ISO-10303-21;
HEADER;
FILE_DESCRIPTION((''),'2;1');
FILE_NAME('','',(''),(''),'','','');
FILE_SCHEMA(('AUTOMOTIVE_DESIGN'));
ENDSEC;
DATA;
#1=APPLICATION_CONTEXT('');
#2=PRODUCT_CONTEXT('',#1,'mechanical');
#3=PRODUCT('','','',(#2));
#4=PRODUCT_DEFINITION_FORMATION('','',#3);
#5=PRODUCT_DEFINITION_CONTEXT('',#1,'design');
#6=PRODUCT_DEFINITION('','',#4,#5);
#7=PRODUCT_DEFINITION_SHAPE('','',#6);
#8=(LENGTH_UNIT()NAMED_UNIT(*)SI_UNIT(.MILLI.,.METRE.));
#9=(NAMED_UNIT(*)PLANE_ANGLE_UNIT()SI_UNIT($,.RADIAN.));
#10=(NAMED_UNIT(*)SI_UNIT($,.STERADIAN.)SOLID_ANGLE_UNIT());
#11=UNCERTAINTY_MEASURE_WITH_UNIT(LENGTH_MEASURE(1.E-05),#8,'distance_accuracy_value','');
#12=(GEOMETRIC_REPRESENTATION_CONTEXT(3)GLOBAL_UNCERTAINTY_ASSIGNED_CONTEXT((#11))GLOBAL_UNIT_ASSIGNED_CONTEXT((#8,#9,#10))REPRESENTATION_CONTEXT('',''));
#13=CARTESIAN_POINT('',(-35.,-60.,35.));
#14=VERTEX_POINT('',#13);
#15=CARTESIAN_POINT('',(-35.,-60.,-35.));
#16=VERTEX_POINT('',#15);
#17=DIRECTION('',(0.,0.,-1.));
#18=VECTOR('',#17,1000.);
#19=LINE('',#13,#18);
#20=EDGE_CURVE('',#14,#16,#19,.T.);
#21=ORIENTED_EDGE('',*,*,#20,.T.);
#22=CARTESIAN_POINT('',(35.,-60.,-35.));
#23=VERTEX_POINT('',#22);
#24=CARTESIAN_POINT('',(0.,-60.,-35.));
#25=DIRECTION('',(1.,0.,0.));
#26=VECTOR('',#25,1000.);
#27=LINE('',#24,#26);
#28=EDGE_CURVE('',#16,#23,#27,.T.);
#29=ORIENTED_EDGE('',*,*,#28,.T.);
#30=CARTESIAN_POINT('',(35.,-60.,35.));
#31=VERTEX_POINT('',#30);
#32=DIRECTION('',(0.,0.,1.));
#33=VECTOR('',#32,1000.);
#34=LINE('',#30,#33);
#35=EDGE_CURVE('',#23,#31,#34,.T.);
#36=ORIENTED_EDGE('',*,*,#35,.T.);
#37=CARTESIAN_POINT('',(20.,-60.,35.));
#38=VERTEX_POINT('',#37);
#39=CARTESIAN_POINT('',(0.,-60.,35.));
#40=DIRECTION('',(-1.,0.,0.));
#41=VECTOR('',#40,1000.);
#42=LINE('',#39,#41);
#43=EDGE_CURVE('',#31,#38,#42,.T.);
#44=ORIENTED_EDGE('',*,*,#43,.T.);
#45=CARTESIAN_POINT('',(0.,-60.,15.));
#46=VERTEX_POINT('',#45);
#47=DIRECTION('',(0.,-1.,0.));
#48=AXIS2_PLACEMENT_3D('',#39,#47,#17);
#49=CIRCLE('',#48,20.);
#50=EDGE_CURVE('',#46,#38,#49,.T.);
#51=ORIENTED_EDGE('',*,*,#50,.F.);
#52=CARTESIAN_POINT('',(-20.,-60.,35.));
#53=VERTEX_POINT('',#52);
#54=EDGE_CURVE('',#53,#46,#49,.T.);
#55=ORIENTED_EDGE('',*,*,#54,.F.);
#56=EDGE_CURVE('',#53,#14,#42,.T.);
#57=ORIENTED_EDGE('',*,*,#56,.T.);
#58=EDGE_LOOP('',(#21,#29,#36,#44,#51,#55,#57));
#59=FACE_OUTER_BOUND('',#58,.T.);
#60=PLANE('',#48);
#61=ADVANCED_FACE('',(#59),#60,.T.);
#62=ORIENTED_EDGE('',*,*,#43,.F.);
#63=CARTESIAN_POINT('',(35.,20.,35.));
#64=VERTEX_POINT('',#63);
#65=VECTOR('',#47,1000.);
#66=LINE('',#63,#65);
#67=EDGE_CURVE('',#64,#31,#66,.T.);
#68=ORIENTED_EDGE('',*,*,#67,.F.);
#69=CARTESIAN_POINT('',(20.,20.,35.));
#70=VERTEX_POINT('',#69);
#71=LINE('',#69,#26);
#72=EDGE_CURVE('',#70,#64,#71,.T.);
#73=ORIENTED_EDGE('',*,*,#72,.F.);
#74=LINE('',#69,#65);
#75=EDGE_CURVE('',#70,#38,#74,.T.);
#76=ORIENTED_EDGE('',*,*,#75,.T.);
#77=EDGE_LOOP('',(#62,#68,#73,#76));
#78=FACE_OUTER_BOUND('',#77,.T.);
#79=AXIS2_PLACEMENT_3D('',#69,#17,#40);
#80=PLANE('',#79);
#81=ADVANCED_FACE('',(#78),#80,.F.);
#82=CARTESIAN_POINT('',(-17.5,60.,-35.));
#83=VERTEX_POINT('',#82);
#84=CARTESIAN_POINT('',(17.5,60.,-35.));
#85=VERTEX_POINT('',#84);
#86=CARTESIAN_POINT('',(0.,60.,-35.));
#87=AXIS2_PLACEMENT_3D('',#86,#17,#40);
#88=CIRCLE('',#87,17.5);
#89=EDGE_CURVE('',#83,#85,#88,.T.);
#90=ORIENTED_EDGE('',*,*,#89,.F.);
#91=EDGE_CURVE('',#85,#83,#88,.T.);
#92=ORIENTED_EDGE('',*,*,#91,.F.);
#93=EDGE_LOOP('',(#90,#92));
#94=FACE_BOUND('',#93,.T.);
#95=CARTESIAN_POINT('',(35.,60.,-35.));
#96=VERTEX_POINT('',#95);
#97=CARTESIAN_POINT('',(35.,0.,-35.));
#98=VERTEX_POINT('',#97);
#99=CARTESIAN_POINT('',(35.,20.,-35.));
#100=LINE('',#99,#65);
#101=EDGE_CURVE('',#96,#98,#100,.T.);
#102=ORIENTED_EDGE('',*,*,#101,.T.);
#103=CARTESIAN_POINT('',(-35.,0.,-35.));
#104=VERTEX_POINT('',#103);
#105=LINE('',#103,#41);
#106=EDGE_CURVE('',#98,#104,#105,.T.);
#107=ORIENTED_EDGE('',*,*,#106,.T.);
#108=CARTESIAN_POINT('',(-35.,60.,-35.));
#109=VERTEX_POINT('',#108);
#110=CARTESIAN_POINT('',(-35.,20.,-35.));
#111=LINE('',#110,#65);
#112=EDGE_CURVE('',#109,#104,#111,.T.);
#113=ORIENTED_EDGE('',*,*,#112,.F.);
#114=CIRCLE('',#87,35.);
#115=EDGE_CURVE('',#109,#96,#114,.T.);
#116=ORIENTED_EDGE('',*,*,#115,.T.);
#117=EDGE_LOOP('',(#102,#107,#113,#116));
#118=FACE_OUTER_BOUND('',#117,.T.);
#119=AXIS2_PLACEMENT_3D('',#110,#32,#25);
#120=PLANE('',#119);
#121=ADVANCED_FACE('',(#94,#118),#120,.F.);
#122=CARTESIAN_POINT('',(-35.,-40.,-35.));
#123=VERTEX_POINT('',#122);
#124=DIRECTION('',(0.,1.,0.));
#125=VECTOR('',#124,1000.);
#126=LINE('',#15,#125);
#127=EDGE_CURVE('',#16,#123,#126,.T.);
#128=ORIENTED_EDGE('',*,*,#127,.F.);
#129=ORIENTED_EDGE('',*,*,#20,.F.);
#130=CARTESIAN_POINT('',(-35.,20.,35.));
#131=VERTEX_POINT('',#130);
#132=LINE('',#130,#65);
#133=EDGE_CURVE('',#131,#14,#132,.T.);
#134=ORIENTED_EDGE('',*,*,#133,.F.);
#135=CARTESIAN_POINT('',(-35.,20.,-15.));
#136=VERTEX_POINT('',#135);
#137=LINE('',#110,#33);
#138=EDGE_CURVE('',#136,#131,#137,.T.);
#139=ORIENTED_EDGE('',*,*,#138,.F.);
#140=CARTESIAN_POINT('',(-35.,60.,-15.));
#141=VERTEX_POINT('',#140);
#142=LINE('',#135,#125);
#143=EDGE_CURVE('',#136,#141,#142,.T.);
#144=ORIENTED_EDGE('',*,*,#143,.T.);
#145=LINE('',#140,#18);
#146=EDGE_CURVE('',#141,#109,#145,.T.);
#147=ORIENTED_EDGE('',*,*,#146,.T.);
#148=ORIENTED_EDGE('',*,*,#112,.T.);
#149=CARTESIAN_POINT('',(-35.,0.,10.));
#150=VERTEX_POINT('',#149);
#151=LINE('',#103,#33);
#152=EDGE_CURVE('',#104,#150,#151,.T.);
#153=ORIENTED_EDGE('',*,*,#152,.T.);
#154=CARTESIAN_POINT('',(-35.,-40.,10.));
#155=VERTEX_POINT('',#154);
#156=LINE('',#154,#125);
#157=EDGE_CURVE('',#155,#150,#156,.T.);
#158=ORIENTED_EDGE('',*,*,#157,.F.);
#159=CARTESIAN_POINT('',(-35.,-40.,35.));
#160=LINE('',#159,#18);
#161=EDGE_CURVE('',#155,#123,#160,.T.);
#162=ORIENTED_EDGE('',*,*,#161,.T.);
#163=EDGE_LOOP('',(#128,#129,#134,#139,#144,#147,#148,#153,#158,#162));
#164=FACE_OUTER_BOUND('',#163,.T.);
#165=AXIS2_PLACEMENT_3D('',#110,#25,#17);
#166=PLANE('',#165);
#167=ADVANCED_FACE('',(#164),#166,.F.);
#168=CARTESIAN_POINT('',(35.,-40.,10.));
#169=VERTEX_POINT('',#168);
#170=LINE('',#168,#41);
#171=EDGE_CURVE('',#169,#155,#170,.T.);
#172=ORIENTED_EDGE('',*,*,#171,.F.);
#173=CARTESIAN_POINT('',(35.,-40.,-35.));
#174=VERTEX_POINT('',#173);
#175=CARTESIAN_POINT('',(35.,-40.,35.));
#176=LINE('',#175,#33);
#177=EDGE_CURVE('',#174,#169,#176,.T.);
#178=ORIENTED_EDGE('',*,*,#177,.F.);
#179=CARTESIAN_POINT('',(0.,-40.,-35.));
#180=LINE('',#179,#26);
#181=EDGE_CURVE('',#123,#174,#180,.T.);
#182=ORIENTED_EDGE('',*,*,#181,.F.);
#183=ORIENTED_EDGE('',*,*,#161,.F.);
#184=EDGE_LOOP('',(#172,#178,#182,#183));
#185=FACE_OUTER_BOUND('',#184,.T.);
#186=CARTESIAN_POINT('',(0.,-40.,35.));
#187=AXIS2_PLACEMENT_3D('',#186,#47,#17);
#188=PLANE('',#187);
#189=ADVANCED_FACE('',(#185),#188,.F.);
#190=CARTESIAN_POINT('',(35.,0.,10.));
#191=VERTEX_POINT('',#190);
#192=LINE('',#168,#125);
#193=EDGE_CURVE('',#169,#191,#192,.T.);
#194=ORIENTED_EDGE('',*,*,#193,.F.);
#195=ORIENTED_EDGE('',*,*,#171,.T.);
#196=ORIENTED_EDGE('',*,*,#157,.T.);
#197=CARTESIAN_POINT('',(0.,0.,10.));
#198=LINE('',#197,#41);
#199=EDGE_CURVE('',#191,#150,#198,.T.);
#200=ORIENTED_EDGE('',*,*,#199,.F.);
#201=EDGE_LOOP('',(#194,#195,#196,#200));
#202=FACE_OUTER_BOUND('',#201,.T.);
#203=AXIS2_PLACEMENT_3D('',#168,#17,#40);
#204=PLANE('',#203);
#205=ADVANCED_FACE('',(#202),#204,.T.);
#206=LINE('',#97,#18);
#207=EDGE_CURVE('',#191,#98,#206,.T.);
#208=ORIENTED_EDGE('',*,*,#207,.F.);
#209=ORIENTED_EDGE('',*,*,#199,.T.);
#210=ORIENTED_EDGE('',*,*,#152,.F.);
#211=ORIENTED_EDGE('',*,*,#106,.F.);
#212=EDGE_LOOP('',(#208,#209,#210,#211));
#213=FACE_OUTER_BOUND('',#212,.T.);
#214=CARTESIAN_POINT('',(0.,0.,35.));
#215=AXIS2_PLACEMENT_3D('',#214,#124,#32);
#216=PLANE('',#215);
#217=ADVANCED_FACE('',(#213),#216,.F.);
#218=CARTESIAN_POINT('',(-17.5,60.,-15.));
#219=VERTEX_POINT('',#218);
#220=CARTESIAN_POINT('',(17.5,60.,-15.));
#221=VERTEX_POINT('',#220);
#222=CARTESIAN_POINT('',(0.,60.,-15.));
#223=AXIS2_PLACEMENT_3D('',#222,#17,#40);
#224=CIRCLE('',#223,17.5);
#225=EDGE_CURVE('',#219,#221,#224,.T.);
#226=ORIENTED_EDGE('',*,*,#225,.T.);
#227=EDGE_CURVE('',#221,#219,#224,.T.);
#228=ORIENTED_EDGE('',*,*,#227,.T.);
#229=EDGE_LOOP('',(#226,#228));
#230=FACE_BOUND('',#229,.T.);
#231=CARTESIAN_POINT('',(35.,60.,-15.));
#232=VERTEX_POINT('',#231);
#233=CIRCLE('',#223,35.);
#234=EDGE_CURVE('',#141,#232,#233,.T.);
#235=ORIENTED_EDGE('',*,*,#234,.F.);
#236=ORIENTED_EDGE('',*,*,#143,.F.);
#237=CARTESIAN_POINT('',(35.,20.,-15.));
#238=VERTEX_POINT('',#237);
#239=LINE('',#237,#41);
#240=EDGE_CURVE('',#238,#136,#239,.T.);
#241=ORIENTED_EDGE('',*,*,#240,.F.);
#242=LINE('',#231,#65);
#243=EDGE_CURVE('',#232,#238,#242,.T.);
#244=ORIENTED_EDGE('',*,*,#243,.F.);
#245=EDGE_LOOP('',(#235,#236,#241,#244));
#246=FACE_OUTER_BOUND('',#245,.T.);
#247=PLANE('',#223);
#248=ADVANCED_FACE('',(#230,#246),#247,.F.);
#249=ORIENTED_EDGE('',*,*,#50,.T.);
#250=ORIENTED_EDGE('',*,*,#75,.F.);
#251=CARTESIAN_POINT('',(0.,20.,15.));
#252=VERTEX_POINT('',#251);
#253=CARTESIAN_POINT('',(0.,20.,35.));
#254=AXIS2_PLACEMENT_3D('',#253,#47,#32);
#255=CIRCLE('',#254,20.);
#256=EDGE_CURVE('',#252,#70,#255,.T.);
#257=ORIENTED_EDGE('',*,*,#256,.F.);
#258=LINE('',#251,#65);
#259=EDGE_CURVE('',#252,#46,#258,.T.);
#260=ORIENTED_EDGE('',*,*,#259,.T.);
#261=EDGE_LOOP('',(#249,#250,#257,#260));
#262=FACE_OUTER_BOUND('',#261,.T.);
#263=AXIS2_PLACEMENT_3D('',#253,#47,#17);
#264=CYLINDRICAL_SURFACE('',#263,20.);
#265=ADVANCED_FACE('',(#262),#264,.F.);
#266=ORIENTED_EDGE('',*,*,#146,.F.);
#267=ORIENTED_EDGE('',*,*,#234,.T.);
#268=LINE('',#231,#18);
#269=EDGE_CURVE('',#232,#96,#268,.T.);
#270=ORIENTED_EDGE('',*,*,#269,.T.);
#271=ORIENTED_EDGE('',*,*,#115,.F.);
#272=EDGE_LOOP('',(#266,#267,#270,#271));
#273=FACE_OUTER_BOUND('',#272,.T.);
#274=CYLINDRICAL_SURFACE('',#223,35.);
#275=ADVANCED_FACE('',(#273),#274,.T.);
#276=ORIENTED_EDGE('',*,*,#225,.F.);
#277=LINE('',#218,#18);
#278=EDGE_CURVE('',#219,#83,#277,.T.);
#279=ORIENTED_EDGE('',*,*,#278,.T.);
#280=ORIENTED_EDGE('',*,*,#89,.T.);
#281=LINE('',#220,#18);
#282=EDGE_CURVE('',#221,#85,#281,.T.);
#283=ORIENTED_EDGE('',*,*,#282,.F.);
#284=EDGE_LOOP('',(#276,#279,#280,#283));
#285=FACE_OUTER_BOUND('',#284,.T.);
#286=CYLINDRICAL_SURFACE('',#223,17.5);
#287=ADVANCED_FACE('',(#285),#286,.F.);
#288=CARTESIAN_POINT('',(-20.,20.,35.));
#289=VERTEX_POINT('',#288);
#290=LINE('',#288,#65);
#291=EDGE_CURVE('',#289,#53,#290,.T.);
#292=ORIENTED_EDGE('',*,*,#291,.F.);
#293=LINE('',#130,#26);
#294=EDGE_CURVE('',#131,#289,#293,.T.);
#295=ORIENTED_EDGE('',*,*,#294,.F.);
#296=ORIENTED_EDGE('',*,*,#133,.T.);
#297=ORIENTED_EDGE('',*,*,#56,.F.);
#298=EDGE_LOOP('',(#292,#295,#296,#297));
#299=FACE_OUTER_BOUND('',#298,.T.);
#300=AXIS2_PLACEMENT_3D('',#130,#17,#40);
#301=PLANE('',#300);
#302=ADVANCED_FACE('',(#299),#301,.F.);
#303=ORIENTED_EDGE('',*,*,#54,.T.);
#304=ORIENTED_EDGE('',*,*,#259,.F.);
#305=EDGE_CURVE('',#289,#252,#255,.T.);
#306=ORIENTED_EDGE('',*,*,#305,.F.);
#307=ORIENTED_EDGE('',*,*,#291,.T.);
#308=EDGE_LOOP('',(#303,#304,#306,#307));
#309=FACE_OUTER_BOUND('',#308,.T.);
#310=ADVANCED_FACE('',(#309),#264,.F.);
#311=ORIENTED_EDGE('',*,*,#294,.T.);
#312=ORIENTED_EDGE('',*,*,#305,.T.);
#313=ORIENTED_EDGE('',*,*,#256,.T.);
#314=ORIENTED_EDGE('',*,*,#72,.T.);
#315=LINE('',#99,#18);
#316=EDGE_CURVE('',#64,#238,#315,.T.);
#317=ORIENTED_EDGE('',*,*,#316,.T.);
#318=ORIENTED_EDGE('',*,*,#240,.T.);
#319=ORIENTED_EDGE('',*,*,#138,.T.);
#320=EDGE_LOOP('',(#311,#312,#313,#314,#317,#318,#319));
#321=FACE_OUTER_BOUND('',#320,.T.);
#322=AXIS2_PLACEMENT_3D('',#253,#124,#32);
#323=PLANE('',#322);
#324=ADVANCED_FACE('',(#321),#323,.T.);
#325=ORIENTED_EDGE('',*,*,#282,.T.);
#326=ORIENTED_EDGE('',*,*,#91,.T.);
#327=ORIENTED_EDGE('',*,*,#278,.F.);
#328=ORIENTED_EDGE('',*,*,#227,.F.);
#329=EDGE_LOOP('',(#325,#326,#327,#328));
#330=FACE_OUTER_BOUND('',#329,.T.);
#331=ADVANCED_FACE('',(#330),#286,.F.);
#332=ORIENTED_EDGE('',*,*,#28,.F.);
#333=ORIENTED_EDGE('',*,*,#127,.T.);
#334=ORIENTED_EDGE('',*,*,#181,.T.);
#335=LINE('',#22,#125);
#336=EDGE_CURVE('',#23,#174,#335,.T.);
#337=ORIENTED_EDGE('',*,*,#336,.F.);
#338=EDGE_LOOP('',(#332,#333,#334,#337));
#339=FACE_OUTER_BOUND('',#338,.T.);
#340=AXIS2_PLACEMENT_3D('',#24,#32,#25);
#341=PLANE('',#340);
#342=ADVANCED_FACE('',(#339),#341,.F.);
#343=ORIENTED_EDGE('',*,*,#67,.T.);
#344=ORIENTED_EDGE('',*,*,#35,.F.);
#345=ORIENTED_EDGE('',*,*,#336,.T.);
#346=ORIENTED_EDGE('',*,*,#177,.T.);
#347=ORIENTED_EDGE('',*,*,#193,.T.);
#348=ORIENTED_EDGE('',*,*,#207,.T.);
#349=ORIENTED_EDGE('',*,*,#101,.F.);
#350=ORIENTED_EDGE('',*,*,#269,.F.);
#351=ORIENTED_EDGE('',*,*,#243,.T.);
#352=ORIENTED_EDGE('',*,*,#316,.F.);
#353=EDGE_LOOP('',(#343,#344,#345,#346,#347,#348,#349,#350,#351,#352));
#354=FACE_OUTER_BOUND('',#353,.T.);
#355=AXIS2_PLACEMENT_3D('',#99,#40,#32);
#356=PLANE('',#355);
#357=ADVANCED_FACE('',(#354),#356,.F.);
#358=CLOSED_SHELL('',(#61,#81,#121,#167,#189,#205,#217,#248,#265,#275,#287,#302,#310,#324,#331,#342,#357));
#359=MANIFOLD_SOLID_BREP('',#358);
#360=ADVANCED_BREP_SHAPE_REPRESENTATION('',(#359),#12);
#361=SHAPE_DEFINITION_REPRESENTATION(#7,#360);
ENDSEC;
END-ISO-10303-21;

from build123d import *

# Parameters (mm, degrees)
LOWER_BODY_BLOCK_DEPTH = 20
UPRIGHT_START          = -60
UPRIGHT_WEB_DEPTH      = 60
UPPER_START            = -60
UPPER_BODY_BLOCK_DEPTH = 20
LIFTING_EYE_SKETCH_R   = 17.5
LIFTING_EYE_LUG_DEPTH  = 20


with BuildPart() as part:
    # Body Block Profile Sketch → Lower Body Block (new body)
    with BuildSketch(Plane(origin=(0, 0, 0), x_dir=(1, 0, 0), z_dir=(0, 1, 0))):
        with BuildLine():
            Line((20, -35), (35, -35))
            Line((35, -35), (35, 35))
            Line((35, 35), (-35, 35))
            Line((-35, 35), (-35, -35))
            Line((-35, -35), (-20, -35))
            ThreePointArc((-20, -35), (0, -15), (20, -35))
        make_face()
    extrude(amount=LOWER_BODY_BLOCK_DEPTH)

    # Upright Web Sketch → Upright Web (add)
    with BuildSketch(Plane(origin=(0, 20, 0), x_dir=(1, 0, 0), z_dir=(0, 1, 0)).offset(UPRIGHT_START)):
        with BuildLine():
            Line((-35, -35), (-20, -35))
            ThreePointArc((-20, -35), (0, -15), (20, -35))
            Line((20, -35), (35, -35))
            Line((35, -35), (35, -10))
            Line((35, -10), (-35, -10))
            Line((-35, -10), (-35, -35))
        make_face()
    extrude(amount=UPRIGHT_WEB_DEPTH)

    # Sketch2_2 → Upper Body Block (add)
    with BuildSketch(Plane(origin=(0, 0, 0), x_dir=(1, 0, 0), z_dir=(0, 1, 0)).offset(UPPER_START)):
        with BuildLine():
            Line((20, -35), (35, -35))
            Line((35, -35), (35, 35))
            Line((35, 35), (-35, 35))
            Line((-35, 35), (-35, -35))
            Line((-35, -35), (-20, -35))
            ThreePointArc((-20, -35), (0, -15), (20, -35))
        make_face()
    extrude(amount=UPPER_BODY_BLOCK_DEPTH)

    # Lifting Eye Sketch → Lifting Eye Lug (add)
    with BuildSketch(Plane(origin=(0, 0, -35), x_dir=(-1, 0, 0), z_dir=(0, 0, -1))):
        with BuildLine():
            Line((-35, 60), (-35, 20))
            Line((-35, 20), (35, 20))
            Line((35, 20), (35, 60))
            ThreePointArc((35, 60), (0, 95), (-35, 60))
        make_face()
        with Locations((0, 60)):
            Circle(LIFTING_EYE_SKETCH_R, mode=Mode.SUBTRACT)
    extrude(amount=-LIFTING_EYE_LUG_DEPTH)


solid = part.part
